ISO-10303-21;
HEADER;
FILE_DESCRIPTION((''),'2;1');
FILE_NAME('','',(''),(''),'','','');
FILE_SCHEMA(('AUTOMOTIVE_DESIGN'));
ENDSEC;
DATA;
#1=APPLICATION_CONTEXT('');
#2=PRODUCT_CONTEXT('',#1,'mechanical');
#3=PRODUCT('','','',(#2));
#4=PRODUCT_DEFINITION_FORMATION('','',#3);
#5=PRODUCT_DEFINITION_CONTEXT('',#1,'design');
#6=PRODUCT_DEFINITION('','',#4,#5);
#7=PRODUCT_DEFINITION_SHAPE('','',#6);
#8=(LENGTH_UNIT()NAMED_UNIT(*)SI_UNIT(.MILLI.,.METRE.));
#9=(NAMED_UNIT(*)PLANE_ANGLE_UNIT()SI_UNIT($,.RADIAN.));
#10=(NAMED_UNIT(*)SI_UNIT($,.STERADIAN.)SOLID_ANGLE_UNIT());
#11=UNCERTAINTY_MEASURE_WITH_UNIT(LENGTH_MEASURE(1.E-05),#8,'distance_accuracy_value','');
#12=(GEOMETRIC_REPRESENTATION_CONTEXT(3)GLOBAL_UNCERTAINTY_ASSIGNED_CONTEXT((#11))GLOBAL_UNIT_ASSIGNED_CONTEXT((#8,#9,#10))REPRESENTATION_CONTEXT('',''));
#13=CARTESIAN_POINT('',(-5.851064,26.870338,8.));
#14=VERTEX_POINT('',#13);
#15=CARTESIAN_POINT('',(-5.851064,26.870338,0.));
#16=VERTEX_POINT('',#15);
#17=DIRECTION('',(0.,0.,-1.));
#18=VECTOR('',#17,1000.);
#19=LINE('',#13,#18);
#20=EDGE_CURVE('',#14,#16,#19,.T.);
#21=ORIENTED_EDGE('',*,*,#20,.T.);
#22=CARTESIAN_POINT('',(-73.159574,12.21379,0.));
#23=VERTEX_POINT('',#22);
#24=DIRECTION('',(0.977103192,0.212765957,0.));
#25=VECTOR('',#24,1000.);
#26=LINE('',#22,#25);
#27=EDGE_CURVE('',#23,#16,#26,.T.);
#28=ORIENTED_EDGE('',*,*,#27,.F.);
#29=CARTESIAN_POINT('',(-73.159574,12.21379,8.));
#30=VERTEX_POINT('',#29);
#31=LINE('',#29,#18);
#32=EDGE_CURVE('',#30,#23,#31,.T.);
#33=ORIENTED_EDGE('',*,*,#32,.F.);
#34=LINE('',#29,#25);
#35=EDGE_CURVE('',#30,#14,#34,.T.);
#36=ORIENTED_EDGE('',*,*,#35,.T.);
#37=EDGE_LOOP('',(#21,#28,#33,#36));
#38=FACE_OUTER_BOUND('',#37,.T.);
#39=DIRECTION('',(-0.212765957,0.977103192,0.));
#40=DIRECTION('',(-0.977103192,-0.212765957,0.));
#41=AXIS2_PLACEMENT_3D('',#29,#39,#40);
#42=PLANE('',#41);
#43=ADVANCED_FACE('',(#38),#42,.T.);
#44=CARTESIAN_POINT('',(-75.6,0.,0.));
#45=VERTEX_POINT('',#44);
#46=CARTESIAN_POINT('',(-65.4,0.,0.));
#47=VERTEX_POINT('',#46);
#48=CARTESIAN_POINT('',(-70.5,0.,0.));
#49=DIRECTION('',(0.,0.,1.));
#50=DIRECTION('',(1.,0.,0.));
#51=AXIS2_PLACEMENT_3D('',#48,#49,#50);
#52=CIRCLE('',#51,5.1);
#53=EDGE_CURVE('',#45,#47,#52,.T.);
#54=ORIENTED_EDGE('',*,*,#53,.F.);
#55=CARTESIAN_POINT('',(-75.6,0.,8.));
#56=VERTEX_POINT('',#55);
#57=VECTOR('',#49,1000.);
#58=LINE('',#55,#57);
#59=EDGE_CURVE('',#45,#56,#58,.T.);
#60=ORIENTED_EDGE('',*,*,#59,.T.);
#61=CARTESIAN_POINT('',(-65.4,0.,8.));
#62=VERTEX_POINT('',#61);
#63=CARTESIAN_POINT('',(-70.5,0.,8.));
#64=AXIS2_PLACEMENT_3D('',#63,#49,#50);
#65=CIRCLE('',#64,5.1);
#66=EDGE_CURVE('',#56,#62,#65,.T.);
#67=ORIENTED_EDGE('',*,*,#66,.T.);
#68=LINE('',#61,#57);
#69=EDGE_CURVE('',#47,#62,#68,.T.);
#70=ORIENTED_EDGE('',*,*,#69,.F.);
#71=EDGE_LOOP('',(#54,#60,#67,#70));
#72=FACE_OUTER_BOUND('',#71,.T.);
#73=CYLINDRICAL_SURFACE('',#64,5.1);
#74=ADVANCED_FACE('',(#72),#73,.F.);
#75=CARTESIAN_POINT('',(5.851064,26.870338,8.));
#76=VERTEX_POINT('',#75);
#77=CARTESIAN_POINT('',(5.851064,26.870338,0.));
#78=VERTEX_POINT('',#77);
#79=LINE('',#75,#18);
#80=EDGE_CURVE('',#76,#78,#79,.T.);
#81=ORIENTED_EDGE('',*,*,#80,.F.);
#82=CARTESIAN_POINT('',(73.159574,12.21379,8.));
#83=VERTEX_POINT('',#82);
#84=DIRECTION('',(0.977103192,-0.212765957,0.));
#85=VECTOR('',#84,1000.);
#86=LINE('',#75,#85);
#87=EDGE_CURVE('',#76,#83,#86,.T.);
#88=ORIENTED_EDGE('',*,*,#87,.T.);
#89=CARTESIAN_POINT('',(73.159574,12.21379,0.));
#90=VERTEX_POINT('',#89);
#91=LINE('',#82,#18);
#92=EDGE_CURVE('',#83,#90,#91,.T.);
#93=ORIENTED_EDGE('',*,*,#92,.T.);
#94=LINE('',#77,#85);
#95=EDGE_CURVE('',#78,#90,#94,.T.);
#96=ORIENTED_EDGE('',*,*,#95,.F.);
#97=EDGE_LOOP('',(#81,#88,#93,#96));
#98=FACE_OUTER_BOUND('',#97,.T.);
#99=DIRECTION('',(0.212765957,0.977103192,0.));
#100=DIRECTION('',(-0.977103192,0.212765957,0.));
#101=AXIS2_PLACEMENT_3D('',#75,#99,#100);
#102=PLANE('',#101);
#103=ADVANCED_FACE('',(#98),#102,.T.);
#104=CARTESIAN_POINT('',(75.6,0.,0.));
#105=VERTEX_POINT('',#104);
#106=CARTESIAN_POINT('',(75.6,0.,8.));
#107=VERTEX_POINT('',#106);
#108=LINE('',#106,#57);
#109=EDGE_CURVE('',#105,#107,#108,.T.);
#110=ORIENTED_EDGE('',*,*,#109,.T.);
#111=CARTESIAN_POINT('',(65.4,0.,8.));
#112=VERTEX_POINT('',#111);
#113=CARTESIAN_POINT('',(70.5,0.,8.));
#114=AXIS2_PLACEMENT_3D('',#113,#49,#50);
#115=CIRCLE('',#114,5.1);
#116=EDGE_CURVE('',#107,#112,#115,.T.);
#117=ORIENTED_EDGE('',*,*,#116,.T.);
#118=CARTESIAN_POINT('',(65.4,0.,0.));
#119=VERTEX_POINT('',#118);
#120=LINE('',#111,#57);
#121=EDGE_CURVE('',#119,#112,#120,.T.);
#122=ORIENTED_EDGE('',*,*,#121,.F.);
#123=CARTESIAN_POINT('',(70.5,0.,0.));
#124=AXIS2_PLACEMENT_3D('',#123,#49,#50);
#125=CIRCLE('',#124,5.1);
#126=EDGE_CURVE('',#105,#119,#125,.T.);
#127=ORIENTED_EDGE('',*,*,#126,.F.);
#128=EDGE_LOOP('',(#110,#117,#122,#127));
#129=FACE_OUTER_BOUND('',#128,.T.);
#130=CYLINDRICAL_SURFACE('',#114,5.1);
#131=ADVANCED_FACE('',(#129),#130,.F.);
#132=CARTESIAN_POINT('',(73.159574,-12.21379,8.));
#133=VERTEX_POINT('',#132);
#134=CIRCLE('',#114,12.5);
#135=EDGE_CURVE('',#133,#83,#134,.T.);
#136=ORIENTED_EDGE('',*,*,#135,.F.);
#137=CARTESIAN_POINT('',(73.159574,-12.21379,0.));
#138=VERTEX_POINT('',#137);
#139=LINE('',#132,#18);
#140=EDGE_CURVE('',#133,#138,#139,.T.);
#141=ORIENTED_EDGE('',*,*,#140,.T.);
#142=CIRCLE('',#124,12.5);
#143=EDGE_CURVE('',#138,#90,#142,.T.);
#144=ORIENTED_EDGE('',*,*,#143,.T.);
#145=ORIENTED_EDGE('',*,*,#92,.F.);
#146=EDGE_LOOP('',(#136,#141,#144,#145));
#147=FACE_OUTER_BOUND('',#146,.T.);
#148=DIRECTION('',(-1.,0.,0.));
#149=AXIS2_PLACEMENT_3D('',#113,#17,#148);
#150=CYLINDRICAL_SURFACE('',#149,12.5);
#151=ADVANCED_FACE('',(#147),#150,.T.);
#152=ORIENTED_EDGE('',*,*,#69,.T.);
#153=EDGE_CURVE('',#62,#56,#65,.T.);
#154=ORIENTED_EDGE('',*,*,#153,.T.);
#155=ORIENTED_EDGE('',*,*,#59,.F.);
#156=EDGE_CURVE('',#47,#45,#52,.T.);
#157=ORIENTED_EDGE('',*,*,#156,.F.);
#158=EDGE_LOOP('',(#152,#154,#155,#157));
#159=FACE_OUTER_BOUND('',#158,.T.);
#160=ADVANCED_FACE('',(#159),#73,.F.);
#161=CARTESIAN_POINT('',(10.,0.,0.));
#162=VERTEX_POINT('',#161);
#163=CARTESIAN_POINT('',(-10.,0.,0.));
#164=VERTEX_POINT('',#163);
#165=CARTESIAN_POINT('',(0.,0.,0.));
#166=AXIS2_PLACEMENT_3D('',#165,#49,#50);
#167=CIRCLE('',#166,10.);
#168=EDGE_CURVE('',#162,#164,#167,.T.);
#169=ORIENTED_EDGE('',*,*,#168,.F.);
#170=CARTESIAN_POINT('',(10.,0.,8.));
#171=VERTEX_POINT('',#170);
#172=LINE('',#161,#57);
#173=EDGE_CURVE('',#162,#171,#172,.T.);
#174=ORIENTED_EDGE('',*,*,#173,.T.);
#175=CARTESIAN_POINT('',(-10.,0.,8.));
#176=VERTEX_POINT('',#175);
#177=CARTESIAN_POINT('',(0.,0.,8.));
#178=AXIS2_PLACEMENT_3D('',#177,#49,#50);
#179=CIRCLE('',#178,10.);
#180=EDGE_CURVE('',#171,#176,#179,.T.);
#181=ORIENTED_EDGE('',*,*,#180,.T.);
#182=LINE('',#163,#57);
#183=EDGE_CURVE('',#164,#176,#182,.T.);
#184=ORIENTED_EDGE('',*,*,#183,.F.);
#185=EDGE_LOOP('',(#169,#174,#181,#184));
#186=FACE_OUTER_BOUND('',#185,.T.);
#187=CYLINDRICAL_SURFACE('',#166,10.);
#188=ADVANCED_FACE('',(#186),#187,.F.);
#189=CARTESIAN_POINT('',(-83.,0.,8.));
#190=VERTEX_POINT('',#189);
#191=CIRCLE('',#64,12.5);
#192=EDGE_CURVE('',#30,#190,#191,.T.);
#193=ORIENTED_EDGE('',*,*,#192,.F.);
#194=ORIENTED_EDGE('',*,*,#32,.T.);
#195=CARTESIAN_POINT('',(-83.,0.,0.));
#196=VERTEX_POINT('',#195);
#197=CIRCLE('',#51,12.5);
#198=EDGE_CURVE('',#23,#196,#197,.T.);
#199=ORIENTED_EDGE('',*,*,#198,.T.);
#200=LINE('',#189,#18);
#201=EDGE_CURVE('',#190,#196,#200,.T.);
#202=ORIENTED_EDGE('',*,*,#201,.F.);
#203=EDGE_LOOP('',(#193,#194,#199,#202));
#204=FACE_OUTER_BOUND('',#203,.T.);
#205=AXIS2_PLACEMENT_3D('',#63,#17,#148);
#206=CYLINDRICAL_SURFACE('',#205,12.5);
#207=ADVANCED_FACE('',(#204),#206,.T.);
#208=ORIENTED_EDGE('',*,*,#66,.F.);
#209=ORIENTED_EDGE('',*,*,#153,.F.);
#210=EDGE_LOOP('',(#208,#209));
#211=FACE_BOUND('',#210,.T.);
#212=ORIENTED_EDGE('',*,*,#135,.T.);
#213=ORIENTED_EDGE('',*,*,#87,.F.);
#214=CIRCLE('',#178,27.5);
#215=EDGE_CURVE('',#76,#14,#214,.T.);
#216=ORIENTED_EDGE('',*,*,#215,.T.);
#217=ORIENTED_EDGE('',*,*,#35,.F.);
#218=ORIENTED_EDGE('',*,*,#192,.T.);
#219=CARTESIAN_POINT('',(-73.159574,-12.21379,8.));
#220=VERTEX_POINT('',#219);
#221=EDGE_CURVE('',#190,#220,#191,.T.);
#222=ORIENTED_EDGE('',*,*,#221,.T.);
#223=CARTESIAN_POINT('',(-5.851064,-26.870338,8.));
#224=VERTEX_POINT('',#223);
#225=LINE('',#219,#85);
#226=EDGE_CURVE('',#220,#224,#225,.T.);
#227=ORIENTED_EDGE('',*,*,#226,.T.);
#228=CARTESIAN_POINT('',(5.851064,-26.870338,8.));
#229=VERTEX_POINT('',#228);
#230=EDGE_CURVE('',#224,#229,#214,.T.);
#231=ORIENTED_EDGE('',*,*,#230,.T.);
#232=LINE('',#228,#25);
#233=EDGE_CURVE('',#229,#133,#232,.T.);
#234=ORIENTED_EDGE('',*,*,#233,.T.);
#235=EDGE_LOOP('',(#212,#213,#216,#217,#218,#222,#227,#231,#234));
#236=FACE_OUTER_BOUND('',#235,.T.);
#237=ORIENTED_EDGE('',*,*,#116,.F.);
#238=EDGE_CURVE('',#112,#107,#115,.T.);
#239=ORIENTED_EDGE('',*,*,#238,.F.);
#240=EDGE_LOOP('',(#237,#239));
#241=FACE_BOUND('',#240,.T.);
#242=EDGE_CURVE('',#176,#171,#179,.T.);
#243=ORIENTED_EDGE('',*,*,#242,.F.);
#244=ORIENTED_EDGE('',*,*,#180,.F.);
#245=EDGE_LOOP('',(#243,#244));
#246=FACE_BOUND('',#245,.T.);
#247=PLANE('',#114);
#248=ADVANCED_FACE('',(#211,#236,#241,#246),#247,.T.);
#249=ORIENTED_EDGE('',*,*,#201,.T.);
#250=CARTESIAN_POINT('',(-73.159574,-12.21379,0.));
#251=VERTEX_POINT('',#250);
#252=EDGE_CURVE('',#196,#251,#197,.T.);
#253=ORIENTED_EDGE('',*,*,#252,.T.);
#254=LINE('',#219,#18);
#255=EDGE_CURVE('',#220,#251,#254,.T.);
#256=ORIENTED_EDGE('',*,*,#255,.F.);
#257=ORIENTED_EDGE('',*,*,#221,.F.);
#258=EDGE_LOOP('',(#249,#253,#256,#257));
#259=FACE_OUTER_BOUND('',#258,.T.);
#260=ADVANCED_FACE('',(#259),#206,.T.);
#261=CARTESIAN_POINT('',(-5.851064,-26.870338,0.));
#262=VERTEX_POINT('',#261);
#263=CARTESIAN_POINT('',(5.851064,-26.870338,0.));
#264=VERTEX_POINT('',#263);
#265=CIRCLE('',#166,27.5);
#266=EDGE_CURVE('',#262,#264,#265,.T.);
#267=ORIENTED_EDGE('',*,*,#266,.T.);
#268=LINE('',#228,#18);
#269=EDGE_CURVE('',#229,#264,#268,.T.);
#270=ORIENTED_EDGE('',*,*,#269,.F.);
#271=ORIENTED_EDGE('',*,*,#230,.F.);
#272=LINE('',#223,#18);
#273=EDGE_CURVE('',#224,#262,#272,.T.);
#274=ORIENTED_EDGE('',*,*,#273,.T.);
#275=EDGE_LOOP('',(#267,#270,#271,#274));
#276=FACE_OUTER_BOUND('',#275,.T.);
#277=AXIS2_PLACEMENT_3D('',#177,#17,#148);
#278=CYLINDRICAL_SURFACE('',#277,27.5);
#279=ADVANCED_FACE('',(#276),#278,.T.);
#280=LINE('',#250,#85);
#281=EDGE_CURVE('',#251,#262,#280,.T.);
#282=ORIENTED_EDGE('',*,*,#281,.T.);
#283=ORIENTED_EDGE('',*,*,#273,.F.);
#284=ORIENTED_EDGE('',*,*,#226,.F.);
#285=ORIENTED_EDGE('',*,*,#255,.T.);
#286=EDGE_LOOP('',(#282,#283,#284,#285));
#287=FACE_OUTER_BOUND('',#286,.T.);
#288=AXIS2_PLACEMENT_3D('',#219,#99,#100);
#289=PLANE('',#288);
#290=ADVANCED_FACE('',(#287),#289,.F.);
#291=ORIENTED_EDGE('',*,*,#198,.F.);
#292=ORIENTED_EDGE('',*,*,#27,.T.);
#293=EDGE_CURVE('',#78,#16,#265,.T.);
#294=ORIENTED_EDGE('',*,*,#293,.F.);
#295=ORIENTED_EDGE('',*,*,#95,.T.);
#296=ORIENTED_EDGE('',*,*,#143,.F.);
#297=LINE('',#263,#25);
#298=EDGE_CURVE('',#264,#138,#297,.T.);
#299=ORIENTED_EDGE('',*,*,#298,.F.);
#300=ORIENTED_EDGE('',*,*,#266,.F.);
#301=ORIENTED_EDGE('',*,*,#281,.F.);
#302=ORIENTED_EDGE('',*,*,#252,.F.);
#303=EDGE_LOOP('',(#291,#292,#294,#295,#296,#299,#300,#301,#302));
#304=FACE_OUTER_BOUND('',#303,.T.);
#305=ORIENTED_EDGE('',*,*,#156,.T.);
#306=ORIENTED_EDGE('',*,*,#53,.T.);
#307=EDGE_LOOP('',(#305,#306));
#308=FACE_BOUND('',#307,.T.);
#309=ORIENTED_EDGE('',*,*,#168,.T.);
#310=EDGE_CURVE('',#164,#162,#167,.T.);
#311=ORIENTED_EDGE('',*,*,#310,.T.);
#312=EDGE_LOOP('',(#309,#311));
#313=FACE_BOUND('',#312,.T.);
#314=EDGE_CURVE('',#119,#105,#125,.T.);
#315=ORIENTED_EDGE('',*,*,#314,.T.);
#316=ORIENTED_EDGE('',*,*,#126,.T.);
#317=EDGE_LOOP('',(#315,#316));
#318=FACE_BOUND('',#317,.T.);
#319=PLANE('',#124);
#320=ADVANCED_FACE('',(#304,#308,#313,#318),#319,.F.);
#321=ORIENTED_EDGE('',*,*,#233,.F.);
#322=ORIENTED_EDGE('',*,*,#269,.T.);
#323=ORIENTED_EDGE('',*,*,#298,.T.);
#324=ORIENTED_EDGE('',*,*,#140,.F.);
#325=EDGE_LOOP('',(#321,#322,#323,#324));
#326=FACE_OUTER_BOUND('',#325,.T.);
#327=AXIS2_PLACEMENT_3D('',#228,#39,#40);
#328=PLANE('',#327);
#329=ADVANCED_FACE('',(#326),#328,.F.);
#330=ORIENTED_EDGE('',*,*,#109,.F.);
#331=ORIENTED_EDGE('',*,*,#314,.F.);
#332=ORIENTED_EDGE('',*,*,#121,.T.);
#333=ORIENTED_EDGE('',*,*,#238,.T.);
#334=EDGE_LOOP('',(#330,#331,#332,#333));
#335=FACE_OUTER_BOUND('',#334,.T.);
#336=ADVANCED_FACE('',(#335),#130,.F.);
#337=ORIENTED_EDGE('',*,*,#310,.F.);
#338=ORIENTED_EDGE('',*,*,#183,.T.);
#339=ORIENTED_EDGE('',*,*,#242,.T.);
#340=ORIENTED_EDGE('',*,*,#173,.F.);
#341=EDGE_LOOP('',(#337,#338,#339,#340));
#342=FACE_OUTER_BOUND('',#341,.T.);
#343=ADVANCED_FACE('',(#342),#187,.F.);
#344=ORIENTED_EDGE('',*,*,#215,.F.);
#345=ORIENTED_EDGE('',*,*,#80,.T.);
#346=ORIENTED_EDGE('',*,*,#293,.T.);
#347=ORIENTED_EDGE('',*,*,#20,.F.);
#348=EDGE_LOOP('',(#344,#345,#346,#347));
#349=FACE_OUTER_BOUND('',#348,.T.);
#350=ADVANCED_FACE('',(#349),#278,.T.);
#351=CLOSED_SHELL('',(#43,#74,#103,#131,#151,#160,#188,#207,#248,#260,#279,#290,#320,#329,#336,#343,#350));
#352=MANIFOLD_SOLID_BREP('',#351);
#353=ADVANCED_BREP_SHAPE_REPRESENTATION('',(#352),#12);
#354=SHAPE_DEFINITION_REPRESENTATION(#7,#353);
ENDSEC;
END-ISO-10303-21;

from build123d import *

# Parameters (mm, degrees)
EXTRUDE_1_DEPTH         = 8
HOLE_WIZARD_M12_1_D     = 10.2
HOLE_WIZARD_M12_1_DEPTH = 29.25
HOLE_WIZARD_M12_1_TIP   = 3.064389157
SKETCH_5_R              = 10
CUT_EXTRUDE_1_DEPTH     = 8


with BuildPart() as part:
    # 草图1 → 凸台-拉伸1 (new body)
    with BuildSketch(Plane.XY):
        with BuildLine():
            Line((-73.159574468, 12.213789897), (-5.85106383, 26.870337773))
            ThreePointArc((-5.85106383, 26.870337773), (0, 27.5), (5.85106383, 26.870337773))
            Line((5.85106383, 26.870337773), (73.159574468, 12.213789897))
            ThreePointArc((73.159574468, 12.213789897), (83, 0), (73.159574468, -12.213789897))
            Line((73.159574468, -12.213789897), (5.85106383, -26.870337773))
            ThreePointArc((5.85106383, -26.870337773), (0, -27.5), (-5.85106383, -26.870337773))
            Line((-5.85106383, -26.870337773), (-73.159574468, -12.213789897))
            ThreePointArc((-73.159574468, -12.213789897), (-83, 0), (-73.159574468, 12.213789897))
        make_face()
    extrude(amount=EXTRUDE_1_DEPTH)

    # M12 螺纹孔1
    with Locations(Plane.XY.offset(8)):
        with Locations((-70.5, 0), (70.5, 0)):
            Hole(HOLE_WIZARD_M12_1_D / 2, depth=HOLE_WIZARD_M12_1_DEPTH)
            with Locations((0, 0, -(HOLE_WIZARD_M12_1_DEPTH + HOLE_WIZARD_M12_1_TIP / 2))):  # 118° drill point
                Cone(0, HOLE_WIZARD_M12_1_D / 2, HOLE_WIZARD_M12_1_TIP, mode=Mode.SUBTRACT)

    # 草图5 → 切除-拉伸1 (cut)
    with BuildSketch(Plane.XY.offset(8)):
        Circle(SKETCH_5_R)
    extrude(amount=-CUT_EXTRUDE_1_DEPTH, mode=Mode.SUBTRACT)


solid = part.part
